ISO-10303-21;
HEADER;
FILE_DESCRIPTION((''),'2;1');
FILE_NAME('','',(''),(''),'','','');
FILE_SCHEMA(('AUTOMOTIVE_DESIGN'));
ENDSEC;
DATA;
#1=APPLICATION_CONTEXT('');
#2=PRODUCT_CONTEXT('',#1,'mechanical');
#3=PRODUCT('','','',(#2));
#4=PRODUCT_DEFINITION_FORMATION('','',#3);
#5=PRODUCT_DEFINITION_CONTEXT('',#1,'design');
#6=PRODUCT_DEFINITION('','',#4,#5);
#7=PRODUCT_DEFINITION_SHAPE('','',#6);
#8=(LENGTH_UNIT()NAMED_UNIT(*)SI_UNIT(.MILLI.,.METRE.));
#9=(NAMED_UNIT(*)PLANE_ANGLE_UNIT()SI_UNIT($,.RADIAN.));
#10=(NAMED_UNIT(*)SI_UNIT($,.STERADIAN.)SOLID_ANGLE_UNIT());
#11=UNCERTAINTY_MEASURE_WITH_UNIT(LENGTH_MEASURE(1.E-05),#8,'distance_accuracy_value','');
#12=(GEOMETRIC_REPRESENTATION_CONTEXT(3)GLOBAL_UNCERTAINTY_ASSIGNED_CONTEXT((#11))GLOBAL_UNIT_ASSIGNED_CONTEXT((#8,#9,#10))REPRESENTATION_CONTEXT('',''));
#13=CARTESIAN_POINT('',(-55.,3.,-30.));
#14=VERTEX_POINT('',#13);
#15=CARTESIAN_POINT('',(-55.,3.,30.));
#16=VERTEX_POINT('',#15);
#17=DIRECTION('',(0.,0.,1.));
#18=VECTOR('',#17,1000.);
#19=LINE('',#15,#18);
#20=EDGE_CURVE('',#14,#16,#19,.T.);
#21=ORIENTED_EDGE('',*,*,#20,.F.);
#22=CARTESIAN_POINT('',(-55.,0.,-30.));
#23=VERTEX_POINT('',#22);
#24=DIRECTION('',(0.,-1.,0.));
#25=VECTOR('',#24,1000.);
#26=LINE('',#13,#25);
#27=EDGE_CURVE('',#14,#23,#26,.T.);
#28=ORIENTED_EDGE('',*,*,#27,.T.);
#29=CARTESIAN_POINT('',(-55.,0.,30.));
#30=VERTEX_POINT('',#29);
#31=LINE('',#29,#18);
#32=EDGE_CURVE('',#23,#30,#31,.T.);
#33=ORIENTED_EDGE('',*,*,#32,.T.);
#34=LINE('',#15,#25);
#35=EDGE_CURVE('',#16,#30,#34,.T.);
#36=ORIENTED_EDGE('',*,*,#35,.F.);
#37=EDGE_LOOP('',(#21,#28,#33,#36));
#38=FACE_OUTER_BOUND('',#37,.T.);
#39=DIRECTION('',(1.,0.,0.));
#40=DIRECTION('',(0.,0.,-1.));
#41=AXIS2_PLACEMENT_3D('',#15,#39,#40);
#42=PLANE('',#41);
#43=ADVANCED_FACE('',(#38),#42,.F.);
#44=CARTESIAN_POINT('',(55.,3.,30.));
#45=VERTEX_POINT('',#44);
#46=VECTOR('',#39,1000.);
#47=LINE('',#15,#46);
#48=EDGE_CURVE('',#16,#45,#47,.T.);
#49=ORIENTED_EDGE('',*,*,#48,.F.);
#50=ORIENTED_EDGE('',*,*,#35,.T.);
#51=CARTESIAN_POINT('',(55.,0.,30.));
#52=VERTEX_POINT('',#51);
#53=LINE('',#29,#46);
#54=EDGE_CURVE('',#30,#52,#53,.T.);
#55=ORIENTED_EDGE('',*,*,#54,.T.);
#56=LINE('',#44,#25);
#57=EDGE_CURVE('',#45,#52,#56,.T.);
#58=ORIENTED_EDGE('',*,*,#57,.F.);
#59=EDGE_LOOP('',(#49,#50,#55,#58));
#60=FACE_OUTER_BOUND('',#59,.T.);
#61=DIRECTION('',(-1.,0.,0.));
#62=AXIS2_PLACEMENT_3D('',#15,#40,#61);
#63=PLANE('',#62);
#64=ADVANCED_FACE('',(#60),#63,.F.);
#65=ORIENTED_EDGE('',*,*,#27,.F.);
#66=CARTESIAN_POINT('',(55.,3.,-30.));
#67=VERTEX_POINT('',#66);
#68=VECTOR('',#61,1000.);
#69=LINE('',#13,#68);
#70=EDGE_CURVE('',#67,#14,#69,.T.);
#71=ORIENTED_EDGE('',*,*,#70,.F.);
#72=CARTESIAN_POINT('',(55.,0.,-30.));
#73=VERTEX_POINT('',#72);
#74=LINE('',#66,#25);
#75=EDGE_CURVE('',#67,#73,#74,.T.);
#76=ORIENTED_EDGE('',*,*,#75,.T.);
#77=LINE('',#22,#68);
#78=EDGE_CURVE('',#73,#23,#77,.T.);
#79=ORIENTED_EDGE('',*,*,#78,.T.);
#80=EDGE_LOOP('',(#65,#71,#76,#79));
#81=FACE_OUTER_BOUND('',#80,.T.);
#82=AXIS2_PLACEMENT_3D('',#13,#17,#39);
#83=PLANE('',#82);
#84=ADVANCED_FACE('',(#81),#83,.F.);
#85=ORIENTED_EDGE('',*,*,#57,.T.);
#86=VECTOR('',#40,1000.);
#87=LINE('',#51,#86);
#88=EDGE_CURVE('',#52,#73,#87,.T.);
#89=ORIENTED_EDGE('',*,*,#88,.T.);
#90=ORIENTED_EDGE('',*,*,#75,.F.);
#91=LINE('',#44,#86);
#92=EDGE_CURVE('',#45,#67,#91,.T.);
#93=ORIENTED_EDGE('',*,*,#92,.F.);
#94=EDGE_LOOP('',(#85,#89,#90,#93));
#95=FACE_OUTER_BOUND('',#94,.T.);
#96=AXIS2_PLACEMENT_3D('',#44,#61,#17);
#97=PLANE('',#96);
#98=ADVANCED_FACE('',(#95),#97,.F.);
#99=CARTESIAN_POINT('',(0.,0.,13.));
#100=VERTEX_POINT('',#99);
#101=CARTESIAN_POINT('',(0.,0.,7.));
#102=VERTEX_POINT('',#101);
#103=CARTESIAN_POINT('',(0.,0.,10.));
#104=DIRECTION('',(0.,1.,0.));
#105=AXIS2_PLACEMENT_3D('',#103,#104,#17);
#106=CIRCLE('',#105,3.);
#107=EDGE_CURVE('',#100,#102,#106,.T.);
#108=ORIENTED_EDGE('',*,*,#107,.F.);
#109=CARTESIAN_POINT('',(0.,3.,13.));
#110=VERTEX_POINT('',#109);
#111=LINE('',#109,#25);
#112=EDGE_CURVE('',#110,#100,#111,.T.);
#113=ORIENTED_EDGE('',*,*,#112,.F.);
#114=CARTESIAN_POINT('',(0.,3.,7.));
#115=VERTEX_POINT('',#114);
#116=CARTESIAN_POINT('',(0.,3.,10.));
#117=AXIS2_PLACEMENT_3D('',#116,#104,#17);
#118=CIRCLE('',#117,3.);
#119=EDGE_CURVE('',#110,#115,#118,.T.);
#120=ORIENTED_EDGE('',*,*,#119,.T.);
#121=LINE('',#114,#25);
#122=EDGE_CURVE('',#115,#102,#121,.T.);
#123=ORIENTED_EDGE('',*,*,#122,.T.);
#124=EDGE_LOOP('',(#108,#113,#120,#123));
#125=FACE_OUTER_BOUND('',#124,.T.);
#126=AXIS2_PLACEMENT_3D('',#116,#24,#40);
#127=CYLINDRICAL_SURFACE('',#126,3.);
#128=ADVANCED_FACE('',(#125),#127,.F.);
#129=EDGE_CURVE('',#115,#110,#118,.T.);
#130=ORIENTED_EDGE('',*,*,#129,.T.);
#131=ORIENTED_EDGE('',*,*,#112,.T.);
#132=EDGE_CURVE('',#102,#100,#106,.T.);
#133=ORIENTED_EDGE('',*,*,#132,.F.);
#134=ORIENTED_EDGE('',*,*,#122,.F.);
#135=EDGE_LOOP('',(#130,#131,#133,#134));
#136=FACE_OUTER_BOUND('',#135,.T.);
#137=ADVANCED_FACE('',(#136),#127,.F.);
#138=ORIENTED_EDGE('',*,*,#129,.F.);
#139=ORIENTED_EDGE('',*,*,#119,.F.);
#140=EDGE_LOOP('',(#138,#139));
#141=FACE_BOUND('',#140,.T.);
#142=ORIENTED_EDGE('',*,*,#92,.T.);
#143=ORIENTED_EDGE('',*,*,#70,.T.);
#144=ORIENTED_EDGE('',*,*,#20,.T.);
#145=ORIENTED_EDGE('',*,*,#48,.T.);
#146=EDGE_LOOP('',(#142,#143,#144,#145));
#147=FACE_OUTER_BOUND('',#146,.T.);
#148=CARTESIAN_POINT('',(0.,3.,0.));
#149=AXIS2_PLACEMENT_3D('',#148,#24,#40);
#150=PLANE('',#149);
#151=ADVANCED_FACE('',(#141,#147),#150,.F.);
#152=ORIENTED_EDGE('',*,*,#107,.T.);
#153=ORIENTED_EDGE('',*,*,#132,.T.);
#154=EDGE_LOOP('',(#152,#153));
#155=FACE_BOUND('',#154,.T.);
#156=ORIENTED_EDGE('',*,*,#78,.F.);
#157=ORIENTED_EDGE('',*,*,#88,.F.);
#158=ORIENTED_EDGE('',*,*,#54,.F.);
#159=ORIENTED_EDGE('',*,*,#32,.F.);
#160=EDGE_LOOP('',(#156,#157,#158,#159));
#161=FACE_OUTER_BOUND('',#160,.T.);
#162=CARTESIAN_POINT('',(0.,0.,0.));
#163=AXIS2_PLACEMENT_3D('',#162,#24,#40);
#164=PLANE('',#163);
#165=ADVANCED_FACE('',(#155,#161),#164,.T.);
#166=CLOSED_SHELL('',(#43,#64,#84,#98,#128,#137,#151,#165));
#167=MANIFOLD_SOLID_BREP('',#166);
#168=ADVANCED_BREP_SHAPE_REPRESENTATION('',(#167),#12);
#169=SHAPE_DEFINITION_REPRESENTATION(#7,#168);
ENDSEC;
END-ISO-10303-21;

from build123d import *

# Parameters (mm, degrees)
SKETCH1_W           = 110
SKETCH1_H           = 60
SKETCH1_R           = 3
BOSS_EXTRUDE1_DEPTH = 3


with BuildPart() as part:
    # Sketch1 → Boss-Extrude1 (new body)
    with BuildSketch(Plane(origin=(0, 0, 0), x_dir=(1, 0, 0), z_dir=(0, 1, 0))):
        Rectangle(SKETCH1_W, SKETCH1_H)
        with Locations(Location((0, -10, 0), (0, 0, 270))):
            Circle(SKETCH1_R, mode=Mode.SUBTRACT)
    extrude(amount=BOSS_EXTRUDE1_DEPTH)


solid = part.part
